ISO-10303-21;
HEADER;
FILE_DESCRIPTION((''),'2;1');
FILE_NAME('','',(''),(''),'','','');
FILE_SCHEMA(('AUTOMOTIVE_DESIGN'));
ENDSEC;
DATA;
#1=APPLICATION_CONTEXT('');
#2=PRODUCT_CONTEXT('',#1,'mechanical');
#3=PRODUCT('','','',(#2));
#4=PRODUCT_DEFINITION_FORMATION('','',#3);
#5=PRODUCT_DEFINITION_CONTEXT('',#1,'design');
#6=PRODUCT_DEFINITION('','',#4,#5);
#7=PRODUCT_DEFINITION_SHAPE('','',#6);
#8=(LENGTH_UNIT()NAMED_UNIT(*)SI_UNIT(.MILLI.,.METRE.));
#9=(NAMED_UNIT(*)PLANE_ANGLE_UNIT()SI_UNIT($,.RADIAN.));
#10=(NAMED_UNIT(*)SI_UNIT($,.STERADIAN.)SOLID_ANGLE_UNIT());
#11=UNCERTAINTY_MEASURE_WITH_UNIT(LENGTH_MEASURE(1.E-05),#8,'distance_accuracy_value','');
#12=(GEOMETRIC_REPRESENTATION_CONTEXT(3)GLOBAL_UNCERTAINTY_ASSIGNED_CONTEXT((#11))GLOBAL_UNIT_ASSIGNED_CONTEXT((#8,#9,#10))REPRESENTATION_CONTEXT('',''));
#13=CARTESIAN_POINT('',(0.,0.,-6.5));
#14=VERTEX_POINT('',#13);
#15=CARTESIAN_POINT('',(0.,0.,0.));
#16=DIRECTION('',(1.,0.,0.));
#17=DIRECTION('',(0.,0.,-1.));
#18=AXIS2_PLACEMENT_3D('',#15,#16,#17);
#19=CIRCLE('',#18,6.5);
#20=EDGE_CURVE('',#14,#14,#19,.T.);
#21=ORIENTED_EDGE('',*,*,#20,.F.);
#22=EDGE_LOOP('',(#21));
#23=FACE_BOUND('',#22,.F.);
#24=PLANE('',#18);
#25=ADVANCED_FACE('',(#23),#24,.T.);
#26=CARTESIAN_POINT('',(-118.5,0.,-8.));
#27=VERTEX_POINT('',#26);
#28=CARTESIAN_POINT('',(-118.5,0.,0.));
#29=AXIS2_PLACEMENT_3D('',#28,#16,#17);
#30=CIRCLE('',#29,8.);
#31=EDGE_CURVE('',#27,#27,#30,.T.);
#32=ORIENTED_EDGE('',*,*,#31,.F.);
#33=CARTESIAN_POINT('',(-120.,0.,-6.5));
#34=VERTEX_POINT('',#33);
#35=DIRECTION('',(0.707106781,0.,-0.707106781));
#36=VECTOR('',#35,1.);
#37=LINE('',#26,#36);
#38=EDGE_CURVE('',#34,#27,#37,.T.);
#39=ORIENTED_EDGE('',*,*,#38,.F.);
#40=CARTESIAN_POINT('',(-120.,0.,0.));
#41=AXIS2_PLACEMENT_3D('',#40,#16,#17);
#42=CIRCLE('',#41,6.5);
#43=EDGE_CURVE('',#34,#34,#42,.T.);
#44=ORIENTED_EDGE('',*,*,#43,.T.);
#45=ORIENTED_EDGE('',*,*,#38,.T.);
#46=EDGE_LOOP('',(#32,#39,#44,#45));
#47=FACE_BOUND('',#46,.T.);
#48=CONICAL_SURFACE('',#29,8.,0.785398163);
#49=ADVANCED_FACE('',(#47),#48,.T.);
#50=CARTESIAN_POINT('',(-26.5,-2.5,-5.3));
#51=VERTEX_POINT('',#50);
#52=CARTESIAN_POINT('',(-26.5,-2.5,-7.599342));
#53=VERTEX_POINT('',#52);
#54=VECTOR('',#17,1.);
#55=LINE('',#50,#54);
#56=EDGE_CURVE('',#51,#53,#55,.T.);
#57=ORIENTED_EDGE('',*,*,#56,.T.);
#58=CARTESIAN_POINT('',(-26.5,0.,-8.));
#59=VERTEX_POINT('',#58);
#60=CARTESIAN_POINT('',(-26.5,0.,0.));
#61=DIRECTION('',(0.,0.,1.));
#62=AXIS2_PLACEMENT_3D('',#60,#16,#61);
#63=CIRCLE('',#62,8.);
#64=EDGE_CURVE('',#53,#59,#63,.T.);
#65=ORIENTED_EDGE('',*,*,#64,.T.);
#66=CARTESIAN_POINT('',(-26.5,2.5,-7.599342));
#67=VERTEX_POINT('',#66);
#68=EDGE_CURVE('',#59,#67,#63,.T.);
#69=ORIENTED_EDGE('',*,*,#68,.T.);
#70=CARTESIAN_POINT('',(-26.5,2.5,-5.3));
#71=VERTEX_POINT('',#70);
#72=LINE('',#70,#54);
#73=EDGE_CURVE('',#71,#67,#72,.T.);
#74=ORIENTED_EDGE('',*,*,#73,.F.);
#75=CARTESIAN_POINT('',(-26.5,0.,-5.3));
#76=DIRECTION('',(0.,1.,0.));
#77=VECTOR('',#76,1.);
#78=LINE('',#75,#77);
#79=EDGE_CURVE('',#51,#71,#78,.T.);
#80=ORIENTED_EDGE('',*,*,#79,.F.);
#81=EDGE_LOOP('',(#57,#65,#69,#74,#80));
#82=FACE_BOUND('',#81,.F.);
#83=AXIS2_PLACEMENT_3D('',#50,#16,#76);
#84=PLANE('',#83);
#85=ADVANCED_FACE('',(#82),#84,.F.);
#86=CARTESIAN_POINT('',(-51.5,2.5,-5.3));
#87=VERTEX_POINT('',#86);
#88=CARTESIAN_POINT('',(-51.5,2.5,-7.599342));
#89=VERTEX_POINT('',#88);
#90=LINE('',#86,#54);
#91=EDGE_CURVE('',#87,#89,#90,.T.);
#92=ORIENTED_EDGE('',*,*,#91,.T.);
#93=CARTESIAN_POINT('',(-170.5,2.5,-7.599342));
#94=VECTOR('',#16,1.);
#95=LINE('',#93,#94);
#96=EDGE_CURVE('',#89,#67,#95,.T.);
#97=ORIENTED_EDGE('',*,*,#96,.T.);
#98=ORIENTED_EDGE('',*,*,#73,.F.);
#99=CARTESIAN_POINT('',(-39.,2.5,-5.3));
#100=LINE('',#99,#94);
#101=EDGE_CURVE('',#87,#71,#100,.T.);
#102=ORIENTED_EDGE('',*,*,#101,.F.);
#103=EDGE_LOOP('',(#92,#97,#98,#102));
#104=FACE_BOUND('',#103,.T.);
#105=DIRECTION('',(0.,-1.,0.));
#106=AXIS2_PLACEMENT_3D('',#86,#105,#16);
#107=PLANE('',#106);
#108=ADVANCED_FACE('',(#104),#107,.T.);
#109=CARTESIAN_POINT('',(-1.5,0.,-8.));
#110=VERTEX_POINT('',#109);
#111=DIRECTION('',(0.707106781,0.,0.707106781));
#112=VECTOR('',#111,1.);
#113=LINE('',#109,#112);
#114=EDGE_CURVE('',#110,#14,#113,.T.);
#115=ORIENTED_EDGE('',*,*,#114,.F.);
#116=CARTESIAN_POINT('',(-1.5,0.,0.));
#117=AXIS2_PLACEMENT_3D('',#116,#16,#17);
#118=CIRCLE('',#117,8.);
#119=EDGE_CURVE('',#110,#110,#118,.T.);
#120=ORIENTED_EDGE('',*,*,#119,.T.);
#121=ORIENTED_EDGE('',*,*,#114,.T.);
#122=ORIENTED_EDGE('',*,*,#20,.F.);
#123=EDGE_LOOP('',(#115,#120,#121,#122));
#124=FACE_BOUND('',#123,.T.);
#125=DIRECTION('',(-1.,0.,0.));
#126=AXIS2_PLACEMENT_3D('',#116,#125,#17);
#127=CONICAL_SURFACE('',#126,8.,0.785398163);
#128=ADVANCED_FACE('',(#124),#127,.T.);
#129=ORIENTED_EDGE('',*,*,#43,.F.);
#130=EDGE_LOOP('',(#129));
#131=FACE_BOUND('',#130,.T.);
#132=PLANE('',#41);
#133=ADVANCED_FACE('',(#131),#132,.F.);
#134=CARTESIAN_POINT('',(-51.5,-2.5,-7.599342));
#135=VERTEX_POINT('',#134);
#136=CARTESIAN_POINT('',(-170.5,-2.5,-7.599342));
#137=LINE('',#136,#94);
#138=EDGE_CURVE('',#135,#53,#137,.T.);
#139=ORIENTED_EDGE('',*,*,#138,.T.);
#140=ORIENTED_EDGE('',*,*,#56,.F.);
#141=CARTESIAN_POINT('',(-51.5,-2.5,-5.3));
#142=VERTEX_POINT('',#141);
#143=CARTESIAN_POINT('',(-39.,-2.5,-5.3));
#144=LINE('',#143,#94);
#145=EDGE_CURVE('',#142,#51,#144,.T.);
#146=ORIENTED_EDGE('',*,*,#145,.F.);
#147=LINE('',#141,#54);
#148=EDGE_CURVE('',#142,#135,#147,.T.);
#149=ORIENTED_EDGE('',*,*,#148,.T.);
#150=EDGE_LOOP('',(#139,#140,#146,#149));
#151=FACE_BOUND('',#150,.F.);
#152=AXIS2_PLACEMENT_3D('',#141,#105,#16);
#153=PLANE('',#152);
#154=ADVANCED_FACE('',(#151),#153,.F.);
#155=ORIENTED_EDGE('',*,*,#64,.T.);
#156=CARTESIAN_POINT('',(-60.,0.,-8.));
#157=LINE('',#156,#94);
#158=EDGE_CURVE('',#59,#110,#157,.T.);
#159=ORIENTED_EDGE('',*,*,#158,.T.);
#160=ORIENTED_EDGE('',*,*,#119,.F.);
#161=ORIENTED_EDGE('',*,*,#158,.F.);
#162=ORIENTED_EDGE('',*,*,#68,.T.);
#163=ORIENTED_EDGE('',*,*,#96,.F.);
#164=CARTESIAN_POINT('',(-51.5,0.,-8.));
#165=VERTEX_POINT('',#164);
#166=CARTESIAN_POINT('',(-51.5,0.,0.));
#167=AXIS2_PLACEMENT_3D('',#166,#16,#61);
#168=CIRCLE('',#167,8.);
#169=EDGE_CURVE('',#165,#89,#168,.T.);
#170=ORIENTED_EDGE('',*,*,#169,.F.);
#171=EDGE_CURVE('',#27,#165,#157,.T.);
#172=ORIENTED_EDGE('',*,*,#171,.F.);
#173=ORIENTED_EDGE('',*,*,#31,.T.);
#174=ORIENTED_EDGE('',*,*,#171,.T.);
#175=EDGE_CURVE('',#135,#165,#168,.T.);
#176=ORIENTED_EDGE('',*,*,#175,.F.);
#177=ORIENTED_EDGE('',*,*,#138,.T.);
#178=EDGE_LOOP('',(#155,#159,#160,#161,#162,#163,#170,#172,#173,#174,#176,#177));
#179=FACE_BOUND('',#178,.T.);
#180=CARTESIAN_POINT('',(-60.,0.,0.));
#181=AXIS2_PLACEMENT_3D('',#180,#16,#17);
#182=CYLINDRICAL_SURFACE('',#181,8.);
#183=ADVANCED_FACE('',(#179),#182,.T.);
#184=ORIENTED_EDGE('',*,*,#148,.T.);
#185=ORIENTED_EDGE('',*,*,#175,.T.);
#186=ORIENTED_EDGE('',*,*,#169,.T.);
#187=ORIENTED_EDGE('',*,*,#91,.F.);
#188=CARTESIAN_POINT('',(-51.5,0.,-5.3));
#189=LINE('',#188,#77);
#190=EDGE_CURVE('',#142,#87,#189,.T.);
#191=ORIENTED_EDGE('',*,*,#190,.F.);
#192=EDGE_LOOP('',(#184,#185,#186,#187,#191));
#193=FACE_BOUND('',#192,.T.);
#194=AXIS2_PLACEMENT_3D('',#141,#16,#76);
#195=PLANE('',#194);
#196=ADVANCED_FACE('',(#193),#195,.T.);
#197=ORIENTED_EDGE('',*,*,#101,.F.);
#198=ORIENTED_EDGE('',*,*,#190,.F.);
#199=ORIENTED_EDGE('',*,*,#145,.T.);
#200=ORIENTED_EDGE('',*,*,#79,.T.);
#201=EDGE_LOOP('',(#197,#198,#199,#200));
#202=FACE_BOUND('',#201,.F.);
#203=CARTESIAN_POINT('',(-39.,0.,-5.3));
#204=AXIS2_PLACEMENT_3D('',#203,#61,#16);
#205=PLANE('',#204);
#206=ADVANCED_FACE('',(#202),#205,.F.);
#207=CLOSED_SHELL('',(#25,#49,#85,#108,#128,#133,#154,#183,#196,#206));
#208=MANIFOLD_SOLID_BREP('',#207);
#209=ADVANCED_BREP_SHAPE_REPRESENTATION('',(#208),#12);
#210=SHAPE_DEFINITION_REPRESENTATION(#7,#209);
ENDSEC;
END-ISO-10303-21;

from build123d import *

# Parameters (mm, degrees)
SKETCH1_W               = 120
SKETCH1_H               = 8
CUT_EXTRUDE1_REACH      = 123
CUT_EXTRUDE1_END_RADIUS = 8
SKETCH2_W               = 25
SKETCH2_H               = 5
CHAMFER1_SIZE           = 1.5


with BuildPart() as part:
    # Sketch1 → Revolve1 (revolve)
    with BuildSketch(Plane.XY, mode=Mode.PRIVATE) as revolve1_sk:
        with Locations((-60, 4)):
            Rectangle(SKETCH1_W, SKETCH1_H)
    revolve(revolve1_sk.sketch.rotate(Axis((-120, 0, 0), (1, 0, 0)), 270), axis=Axis((-120, 0, 0), (1, 0, 0)))

    # Cut-Extrude1: up to this cylinder (the profile starts inside it)
    cut_extrude1_end = Plane(origin=(-39, 0, 0), z_dir=(1, 0, 0)) * Cylinder(CUT_EXTRUDE1_END_RADIUS, 263, mode=Mode.PRIVATE)
    # Sketch2 → Cut-Extrude1 (cut, up to the surface)
    with BuildSketch(Plane.XY.offset(-5.3), mode=Mode.PRIVATE) as cut_extrude1_sk1:
        with Locations((-39, 0)):
            Rectangle(SKETCH2_W, SKETCH2_H)
    cut_extrude1_tool1 = extrude(cut_extrude1_sk1.sketch, amount=-CUT_EXTRUDE1_REACH, mode=Mode.PRIVATE) & cut_extrude1_end
    add(cut_extrude1_tool1.solids().sort_by_distance((-39, 0, -5.3))[0], mode=Mode.SUBTRACT)

    # Chamfer1
    chamfer1_edges = [part.edges().sort_by_distance(p)[0] for p in [
        (0, 0, 8),
        (-120, 0, 8),
    ]]
    chamfer(chamfer1_edges, length=CHAMFER1_SIZE)


solid = part.part
